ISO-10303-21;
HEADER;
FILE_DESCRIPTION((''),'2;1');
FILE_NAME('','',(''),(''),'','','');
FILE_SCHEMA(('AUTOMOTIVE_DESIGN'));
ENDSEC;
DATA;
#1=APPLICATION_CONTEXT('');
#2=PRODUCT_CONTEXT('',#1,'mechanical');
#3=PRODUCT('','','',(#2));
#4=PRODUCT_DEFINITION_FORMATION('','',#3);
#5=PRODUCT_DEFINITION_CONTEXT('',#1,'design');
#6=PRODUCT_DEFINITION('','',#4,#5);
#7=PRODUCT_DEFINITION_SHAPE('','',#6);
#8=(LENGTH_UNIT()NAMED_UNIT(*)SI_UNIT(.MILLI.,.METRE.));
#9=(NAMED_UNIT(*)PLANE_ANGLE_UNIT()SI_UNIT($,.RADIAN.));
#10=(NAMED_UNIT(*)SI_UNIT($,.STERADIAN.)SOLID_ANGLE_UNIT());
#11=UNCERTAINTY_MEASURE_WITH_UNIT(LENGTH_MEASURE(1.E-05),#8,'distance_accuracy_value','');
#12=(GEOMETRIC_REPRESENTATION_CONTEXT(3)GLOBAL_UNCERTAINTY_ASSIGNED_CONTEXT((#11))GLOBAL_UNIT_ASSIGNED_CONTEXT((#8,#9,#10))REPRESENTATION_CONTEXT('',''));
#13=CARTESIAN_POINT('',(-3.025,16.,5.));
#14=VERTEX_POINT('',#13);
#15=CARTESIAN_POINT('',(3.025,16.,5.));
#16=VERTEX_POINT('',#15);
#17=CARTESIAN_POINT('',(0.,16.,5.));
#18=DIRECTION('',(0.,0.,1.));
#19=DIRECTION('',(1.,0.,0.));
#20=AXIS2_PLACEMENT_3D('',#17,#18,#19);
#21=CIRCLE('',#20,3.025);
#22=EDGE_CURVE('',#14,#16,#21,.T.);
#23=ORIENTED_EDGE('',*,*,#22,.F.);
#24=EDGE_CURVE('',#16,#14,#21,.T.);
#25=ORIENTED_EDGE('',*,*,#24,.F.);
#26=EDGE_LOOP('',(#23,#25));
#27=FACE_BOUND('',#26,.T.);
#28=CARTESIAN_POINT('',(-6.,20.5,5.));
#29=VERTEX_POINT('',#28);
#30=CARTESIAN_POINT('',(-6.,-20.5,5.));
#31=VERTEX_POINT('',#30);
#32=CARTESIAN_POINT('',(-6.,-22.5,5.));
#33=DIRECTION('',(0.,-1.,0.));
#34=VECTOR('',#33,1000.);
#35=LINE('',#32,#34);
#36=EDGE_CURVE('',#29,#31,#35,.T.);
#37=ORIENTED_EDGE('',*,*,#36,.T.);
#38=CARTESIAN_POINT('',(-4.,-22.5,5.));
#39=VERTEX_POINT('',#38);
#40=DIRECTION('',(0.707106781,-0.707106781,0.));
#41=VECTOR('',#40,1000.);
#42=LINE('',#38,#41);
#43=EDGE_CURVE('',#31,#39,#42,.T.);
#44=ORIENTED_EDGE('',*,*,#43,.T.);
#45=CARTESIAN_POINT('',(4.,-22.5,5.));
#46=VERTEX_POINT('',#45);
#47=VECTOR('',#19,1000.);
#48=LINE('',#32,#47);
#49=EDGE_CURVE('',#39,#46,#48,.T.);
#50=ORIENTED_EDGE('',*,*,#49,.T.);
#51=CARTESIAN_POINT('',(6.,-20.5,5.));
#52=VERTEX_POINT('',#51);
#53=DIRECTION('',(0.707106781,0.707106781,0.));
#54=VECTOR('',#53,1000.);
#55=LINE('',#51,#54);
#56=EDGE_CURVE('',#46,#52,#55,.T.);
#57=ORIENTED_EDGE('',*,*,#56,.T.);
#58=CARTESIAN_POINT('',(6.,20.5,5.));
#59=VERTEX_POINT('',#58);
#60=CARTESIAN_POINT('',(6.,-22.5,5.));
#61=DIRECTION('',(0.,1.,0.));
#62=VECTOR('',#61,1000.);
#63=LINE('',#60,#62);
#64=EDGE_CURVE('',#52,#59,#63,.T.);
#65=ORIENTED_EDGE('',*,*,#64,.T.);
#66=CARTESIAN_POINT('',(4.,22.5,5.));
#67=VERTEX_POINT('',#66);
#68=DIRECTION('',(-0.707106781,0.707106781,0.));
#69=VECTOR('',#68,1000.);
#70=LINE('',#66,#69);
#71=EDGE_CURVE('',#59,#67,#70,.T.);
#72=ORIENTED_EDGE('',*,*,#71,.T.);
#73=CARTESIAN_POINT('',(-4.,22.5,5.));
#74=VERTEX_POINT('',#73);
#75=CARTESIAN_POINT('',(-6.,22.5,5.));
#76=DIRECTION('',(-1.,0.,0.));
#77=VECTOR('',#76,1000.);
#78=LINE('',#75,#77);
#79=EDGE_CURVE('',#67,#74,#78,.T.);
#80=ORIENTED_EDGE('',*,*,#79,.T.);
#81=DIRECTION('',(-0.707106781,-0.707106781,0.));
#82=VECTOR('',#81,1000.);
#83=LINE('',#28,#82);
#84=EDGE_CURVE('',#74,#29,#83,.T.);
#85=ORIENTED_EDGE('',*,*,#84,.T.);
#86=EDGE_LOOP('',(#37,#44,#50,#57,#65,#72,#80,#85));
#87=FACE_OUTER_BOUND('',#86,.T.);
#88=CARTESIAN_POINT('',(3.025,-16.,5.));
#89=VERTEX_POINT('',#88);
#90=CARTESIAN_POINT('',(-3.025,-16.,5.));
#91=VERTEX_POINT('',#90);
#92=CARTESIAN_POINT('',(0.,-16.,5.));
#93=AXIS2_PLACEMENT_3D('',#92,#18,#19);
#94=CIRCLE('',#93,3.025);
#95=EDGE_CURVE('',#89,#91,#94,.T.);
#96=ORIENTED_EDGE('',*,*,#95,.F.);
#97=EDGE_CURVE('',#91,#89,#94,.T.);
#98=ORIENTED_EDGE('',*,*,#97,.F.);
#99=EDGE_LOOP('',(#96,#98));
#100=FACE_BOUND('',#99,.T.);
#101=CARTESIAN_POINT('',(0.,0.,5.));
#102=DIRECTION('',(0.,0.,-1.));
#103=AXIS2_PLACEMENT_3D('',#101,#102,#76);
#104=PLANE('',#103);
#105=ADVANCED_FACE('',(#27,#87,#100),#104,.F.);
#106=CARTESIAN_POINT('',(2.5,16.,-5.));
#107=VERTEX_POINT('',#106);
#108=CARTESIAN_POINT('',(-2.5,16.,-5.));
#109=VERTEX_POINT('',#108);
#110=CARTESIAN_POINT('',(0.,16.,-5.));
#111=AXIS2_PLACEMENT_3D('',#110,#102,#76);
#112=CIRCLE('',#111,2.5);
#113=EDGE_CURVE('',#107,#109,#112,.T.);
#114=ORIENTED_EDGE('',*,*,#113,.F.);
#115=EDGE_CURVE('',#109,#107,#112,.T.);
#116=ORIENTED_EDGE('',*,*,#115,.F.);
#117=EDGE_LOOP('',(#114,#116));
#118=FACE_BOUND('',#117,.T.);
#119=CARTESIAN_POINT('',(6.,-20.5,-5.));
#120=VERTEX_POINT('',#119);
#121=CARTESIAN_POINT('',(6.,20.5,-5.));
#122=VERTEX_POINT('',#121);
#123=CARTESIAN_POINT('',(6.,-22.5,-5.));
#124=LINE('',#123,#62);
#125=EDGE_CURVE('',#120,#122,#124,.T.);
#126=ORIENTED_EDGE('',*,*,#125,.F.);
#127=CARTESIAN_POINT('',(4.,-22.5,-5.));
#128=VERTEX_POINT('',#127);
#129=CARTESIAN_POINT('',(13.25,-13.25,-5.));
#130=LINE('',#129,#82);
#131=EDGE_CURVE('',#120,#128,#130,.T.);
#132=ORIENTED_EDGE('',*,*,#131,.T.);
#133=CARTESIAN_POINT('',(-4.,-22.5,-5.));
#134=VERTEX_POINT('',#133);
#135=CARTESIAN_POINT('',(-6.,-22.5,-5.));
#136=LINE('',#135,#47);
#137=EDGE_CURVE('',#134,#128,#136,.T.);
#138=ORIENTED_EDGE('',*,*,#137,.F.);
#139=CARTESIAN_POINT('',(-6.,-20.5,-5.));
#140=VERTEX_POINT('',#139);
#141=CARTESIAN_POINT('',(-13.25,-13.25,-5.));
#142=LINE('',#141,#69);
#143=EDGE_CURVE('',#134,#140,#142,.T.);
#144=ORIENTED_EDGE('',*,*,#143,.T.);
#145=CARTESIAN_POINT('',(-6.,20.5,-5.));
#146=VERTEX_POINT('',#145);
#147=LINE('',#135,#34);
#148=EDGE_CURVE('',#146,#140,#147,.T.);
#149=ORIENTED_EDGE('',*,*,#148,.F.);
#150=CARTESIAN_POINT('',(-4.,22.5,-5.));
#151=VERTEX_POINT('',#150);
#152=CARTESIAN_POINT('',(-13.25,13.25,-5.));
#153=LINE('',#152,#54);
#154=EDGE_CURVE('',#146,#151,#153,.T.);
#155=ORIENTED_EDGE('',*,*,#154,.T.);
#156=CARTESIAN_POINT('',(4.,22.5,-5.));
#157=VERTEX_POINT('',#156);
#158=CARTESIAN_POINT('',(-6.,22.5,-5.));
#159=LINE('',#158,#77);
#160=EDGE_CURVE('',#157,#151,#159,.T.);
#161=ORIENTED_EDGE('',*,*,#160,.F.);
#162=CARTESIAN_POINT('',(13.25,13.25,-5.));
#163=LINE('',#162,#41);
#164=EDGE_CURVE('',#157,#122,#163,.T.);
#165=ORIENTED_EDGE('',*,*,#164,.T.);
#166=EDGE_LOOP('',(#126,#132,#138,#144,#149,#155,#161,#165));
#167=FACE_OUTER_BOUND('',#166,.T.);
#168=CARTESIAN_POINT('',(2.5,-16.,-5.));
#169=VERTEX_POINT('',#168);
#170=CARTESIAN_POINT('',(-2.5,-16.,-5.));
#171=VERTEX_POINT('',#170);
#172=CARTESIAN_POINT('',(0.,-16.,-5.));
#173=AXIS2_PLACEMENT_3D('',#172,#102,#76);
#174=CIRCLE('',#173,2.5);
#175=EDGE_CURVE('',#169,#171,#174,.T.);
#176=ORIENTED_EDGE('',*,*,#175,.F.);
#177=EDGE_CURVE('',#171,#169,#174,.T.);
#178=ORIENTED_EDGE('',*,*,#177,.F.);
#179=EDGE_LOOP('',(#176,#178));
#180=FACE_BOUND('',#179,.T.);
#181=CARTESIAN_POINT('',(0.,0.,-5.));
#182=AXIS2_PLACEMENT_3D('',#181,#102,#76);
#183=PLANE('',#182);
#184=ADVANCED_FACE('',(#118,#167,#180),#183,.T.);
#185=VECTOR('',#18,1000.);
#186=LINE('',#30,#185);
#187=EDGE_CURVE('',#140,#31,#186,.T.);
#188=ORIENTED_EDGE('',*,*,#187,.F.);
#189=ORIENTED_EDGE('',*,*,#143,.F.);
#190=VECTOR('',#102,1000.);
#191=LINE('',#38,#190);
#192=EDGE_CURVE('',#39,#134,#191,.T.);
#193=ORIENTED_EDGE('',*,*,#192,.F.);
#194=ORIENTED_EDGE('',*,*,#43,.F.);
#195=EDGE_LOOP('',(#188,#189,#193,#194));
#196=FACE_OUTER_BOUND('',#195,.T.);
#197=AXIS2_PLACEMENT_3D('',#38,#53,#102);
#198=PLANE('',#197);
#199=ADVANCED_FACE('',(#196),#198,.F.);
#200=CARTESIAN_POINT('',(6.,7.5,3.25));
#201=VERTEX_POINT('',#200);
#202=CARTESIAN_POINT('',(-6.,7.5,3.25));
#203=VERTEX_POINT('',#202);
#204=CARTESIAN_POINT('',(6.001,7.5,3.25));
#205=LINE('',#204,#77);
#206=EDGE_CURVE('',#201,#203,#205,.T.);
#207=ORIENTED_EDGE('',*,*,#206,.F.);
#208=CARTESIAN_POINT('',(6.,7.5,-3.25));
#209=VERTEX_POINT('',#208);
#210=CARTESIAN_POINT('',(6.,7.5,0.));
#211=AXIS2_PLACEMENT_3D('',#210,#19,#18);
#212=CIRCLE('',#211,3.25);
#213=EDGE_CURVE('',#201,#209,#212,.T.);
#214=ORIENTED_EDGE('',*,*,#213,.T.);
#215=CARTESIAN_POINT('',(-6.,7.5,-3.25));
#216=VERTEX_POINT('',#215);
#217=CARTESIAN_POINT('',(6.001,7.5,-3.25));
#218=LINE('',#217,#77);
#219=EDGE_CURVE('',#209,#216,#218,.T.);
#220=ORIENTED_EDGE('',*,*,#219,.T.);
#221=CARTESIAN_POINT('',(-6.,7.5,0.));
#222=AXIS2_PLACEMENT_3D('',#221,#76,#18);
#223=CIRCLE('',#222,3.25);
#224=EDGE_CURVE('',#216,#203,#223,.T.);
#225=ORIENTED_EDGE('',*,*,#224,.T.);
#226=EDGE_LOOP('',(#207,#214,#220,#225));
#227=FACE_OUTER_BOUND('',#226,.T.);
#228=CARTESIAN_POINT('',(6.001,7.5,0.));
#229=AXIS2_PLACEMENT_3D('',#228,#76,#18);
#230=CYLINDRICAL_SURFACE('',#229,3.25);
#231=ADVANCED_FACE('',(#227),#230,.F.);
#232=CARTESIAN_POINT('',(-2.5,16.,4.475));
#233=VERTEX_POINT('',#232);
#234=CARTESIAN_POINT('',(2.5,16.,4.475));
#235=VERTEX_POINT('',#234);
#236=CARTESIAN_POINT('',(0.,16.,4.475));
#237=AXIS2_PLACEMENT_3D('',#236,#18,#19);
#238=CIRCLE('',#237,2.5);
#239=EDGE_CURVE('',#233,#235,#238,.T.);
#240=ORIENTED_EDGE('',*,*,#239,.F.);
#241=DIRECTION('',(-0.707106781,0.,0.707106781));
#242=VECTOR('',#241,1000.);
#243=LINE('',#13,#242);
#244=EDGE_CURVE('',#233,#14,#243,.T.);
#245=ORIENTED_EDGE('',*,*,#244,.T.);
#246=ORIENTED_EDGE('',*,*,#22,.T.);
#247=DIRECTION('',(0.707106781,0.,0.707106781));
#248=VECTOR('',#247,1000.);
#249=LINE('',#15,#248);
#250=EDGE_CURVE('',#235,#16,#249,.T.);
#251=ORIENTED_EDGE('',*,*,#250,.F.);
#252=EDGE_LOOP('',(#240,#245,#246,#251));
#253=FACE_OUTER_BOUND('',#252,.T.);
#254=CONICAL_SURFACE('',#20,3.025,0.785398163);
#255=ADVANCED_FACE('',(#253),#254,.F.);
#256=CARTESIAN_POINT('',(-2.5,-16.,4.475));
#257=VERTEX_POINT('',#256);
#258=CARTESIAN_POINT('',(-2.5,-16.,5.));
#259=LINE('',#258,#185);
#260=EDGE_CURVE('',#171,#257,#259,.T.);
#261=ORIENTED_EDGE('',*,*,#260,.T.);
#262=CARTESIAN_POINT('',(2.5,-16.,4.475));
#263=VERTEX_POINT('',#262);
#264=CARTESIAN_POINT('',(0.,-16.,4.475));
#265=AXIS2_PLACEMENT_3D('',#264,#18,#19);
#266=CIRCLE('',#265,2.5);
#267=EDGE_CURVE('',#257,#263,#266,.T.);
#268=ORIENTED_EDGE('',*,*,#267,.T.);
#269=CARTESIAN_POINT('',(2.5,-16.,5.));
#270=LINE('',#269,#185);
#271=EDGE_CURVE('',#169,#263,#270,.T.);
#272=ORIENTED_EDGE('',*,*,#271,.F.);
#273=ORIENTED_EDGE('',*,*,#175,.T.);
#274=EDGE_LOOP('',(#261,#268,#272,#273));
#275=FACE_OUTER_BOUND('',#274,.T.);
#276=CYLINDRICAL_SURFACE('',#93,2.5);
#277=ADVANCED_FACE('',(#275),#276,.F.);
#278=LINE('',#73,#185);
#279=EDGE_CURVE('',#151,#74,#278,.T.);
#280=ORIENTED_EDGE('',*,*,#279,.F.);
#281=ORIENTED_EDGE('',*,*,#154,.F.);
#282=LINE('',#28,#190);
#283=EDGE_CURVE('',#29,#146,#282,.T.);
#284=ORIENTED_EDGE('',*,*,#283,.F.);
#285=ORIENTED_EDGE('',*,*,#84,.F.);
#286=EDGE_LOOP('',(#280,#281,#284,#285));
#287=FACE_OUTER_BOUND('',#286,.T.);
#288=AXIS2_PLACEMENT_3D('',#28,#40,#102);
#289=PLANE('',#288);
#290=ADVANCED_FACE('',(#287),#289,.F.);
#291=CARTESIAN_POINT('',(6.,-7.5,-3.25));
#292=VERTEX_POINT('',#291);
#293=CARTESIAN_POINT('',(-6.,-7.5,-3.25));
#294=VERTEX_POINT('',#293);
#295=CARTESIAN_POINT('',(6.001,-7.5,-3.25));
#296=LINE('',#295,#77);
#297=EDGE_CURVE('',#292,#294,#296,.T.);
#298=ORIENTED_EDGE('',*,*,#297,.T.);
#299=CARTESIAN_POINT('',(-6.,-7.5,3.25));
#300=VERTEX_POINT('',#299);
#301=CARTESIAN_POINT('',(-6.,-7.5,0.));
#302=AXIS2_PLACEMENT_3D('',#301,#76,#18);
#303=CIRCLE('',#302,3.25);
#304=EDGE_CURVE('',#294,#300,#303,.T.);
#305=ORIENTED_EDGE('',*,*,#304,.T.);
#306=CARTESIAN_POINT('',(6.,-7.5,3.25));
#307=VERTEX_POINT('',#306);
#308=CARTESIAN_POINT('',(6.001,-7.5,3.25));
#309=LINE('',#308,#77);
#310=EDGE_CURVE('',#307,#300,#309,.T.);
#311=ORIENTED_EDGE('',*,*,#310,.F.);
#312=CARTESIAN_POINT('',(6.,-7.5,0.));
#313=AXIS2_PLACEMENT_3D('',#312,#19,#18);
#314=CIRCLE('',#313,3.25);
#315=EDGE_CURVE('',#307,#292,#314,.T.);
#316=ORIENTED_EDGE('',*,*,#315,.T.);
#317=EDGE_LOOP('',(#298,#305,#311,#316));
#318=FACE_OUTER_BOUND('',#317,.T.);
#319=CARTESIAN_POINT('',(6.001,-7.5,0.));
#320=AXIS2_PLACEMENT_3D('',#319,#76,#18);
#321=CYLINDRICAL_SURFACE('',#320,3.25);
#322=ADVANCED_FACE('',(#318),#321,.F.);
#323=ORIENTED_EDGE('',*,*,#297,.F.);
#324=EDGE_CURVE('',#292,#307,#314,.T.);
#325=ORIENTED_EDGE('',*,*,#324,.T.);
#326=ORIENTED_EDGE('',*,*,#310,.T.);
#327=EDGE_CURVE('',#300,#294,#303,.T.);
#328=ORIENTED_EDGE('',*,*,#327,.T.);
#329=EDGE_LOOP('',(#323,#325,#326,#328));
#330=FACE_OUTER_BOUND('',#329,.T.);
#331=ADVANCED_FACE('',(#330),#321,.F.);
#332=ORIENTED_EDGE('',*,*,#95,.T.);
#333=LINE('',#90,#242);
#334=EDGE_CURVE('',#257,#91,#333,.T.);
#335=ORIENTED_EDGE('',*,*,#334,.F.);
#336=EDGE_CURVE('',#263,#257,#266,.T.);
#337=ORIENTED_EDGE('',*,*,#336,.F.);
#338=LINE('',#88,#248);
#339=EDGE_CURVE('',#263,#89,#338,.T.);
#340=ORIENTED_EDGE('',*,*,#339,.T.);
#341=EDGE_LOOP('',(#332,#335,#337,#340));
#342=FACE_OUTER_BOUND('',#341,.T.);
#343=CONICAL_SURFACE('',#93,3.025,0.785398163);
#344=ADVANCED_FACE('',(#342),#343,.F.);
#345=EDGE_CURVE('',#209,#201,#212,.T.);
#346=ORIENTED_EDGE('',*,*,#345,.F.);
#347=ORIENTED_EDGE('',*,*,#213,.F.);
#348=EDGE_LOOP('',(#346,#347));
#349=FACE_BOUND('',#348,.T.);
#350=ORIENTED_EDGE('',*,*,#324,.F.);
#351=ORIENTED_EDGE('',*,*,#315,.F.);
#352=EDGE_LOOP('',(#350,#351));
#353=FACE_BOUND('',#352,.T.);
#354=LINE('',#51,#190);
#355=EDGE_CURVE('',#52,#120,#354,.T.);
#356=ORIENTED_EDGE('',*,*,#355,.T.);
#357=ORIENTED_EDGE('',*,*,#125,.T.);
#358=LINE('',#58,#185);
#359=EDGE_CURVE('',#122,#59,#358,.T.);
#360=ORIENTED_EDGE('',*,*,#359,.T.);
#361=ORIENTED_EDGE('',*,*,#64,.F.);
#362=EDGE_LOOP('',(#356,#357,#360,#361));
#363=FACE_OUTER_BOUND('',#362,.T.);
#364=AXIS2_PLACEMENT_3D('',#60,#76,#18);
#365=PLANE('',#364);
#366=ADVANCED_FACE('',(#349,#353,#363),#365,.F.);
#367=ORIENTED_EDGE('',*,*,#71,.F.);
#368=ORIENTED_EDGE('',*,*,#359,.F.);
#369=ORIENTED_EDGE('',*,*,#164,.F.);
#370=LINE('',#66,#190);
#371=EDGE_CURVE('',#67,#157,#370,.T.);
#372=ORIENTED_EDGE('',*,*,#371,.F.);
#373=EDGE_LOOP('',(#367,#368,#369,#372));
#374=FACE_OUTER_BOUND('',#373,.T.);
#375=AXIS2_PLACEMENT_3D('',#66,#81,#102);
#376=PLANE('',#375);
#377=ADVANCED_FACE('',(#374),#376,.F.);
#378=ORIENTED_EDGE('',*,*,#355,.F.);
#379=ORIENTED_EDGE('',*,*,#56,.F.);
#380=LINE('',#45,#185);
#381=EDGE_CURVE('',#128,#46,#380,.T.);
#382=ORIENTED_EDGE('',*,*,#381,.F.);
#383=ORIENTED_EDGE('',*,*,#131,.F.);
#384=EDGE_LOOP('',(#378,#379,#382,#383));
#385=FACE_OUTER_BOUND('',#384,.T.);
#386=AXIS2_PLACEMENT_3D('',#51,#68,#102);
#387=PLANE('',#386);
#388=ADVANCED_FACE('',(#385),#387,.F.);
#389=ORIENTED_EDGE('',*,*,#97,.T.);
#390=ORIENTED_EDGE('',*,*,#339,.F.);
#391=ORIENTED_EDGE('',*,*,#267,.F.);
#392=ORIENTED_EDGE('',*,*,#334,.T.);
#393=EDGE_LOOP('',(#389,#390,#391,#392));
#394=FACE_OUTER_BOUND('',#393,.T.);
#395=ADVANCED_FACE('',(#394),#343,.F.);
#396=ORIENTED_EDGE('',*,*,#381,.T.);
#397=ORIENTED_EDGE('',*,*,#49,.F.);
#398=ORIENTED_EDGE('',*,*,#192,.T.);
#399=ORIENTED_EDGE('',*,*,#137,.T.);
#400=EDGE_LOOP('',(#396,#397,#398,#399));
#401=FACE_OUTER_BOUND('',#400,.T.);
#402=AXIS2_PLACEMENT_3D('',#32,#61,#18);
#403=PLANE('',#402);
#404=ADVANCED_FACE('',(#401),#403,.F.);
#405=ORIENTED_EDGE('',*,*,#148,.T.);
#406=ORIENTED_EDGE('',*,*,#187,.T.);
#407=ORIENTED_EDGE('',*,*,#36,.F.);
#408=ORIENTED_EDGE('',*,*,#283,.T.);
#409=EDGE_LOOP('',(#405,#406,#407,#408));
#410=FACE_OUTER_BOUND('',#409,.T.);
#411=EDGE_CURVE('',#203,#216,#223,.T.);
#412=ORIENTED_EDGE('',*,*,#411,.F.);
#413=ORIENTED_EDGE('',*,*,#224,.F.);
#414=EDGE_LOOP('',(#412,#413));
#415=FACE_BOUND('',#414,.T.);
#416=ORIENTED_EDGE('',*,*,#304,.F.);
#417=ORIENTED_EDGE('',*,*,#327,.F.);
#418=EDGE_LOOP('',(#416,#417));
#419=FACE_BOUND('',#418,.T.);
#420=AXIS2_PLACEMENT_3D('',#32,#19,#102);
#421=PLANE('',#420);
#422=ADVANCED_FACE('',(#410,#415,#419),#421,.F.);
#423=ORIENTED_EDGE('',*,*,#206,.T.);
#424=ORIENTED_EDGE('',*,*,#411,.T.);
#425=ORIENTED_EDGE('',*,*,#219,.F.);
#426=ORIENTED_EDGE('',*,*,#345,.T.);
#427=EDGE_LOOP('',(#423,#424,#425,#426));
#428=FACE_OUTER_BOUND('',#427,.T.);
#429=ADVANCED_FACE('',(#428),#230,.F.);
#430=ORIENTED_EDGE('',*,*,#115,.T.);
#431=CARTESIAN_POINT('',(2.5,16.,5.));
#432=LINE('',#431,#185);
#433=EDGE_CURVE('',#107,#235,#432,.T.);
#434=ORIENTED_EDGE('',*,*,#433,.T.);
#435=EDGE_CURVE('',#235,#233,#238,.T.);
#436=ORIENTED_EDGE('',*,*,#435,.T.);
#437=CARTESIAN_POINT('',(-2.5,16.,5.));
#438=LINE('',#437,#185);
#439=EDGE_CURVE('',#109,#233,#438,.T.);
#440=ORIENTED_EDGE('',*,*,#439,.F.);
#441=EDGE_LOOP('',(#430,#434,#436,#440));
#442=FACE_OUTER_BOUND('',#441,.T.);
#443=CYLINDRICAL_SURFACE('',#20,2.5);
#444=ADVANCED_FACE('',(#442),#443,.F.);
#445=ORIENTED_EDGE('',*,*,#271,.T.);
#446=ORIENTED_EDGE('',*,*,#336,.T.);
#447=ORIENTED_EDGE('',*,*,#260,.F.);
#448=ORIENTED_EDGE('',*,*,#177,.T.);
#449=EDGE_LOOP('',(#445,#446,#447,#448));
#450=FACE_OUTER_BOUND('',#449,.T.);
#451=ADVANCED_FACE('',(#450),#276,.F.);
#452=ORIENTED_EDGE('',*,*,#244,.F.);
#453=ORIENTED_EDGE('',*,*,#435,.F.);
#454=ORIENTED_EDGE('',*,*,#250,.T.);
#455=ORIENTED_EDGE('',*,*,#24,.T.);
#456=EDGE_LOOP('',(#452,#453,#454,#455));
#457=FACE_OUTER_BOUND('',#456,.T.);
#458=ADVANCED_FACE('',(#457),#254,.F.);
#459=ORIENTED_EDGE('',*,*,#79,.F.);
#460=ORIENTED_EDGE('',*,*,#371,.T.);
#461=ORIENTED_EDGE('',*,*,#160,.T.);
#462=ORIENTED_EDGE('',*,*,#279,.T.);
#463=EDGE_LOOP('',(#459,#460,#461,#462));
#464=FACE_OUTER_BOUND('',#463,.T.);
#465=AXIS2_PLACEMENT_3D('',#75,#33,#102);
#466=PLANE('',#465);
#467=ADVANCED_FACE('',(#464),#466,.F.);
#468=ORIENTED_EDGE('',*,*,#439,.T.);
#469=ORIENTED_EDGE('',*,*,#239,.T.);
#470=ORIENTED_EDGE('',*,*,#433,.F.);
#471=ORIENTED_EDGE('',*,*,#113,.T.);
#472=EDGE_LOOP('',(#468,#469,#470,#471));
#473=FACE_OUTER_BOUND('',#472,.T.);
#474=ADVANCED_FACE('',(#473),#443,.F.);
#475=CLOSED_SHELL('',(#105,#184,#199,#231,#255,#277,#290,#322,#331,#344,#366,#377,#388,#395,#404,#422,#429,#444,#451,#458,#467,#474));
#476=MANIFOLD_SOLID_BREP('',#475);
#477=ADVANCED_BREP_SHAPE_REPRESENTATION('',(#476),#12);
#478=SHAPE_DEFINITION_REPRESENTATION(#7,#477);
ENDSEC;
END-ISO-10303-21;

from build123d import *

# Parameters (mm, degrees)
SKETCH_1_W                   = 12
SKETCH_1_H                   = 45
EXTRUDE_1_DEPTH              = 5
HOLE_WIZARD_M6_1_D           = 5
HOLE_WIZARD_M6_1_CSINK_D     = 6.05
HOLE_WIZARD_M6_1_CSINK_ANGLE = 90
CUT_EXTRUDE_1_REACH          = 27.986
SKETCH_3_R                   = 3.25
CHAMFER_1_SIZE               = 2


with BuildPart() as part:
    # 草图1 → 凸台-拉伸1 (new, symmetric)
    with BuildSketch(Plane.XY):
        Rectangle(SKETCH_1_W, SKETCH_1_H)
    extrude(amount=EXTRUDE_1_DEPTH, both=True)

    # M6 螺纹孔1 (through all)
    with Locations(Plane(origin=(0, -16, 5), x_dir=(1, 0, 0), z_dir=(0, 0, 1))):
        with Locations((0, 0)):
            hole_wizard_m6_1 = CounterSinkHole(HOLE_WIZARD_M6_1_D / 2, HOLE_WIZARD_M6_1_CSINK_D / 2, counter_sink_angle=HOLE_WIZARD_M6_1_CSINK_ANGLE)

    # 草图3 → 切除-拉伸1 (cut, up to next)
    with BuildSketch(Plane.ZY.offset(6), mode=Mode.PRIVATE) as cut_extrude_1_sk1:
        with Locations((0, 7.5)):
            Circle(SKETCH_3_R)
    cut_extrude_1_tool1 = extrude(cut_extrude_1_sk1.sketch, amount=-CUT_EXTRUDE_1_REACH, mode=Mode.PRIVATE) & part.part
    # 草图3 → 切除-拉伸1 (cut, up to next)
    with BuildSketch(Plane.ZY.offset(6), mode=Mode.PRIVATE) as cut_extrude_1_sk2:
        with Locations((0, -7.5)):
            Circle(SKETCH_3_R)
    cut_extrude_1_tool2 = extrude(cut_extrude_1_sk2.sketch, amount=-CUT_EXTRUDE_1_REACH, mode=Mode.PRIVATE) & part.part
    add(cut_extrude_1_tool1.solids().sort_by_distance((-6, 7.5, 0))[0], mode=Mode.SUBTRACT)
    add(cut_extrude_1_tool2.solids().sort_by_distance((-6, -7.5, 0))[0], mode=Mode.SUBTRACT)

    # 镜向1: M6 螺纹孔1 across plane
    add(hole_wizard_m6_1.mirror(Plane.ZX), mode=Mode.SUBTRACT)

    # 倒角1
    chamfer_1_edges = [part.edges().sort_by_distance(p)[0] for p in [
        (6, -22.5, 0),
        (-6, -22.5, 0),
        (-6, 22.5, 0),
        (6, 22.5, 0),
    ]]
    chamfer(chamfer_1_edges, length=CHAMFER_1_SIZE)


solid = part.part
